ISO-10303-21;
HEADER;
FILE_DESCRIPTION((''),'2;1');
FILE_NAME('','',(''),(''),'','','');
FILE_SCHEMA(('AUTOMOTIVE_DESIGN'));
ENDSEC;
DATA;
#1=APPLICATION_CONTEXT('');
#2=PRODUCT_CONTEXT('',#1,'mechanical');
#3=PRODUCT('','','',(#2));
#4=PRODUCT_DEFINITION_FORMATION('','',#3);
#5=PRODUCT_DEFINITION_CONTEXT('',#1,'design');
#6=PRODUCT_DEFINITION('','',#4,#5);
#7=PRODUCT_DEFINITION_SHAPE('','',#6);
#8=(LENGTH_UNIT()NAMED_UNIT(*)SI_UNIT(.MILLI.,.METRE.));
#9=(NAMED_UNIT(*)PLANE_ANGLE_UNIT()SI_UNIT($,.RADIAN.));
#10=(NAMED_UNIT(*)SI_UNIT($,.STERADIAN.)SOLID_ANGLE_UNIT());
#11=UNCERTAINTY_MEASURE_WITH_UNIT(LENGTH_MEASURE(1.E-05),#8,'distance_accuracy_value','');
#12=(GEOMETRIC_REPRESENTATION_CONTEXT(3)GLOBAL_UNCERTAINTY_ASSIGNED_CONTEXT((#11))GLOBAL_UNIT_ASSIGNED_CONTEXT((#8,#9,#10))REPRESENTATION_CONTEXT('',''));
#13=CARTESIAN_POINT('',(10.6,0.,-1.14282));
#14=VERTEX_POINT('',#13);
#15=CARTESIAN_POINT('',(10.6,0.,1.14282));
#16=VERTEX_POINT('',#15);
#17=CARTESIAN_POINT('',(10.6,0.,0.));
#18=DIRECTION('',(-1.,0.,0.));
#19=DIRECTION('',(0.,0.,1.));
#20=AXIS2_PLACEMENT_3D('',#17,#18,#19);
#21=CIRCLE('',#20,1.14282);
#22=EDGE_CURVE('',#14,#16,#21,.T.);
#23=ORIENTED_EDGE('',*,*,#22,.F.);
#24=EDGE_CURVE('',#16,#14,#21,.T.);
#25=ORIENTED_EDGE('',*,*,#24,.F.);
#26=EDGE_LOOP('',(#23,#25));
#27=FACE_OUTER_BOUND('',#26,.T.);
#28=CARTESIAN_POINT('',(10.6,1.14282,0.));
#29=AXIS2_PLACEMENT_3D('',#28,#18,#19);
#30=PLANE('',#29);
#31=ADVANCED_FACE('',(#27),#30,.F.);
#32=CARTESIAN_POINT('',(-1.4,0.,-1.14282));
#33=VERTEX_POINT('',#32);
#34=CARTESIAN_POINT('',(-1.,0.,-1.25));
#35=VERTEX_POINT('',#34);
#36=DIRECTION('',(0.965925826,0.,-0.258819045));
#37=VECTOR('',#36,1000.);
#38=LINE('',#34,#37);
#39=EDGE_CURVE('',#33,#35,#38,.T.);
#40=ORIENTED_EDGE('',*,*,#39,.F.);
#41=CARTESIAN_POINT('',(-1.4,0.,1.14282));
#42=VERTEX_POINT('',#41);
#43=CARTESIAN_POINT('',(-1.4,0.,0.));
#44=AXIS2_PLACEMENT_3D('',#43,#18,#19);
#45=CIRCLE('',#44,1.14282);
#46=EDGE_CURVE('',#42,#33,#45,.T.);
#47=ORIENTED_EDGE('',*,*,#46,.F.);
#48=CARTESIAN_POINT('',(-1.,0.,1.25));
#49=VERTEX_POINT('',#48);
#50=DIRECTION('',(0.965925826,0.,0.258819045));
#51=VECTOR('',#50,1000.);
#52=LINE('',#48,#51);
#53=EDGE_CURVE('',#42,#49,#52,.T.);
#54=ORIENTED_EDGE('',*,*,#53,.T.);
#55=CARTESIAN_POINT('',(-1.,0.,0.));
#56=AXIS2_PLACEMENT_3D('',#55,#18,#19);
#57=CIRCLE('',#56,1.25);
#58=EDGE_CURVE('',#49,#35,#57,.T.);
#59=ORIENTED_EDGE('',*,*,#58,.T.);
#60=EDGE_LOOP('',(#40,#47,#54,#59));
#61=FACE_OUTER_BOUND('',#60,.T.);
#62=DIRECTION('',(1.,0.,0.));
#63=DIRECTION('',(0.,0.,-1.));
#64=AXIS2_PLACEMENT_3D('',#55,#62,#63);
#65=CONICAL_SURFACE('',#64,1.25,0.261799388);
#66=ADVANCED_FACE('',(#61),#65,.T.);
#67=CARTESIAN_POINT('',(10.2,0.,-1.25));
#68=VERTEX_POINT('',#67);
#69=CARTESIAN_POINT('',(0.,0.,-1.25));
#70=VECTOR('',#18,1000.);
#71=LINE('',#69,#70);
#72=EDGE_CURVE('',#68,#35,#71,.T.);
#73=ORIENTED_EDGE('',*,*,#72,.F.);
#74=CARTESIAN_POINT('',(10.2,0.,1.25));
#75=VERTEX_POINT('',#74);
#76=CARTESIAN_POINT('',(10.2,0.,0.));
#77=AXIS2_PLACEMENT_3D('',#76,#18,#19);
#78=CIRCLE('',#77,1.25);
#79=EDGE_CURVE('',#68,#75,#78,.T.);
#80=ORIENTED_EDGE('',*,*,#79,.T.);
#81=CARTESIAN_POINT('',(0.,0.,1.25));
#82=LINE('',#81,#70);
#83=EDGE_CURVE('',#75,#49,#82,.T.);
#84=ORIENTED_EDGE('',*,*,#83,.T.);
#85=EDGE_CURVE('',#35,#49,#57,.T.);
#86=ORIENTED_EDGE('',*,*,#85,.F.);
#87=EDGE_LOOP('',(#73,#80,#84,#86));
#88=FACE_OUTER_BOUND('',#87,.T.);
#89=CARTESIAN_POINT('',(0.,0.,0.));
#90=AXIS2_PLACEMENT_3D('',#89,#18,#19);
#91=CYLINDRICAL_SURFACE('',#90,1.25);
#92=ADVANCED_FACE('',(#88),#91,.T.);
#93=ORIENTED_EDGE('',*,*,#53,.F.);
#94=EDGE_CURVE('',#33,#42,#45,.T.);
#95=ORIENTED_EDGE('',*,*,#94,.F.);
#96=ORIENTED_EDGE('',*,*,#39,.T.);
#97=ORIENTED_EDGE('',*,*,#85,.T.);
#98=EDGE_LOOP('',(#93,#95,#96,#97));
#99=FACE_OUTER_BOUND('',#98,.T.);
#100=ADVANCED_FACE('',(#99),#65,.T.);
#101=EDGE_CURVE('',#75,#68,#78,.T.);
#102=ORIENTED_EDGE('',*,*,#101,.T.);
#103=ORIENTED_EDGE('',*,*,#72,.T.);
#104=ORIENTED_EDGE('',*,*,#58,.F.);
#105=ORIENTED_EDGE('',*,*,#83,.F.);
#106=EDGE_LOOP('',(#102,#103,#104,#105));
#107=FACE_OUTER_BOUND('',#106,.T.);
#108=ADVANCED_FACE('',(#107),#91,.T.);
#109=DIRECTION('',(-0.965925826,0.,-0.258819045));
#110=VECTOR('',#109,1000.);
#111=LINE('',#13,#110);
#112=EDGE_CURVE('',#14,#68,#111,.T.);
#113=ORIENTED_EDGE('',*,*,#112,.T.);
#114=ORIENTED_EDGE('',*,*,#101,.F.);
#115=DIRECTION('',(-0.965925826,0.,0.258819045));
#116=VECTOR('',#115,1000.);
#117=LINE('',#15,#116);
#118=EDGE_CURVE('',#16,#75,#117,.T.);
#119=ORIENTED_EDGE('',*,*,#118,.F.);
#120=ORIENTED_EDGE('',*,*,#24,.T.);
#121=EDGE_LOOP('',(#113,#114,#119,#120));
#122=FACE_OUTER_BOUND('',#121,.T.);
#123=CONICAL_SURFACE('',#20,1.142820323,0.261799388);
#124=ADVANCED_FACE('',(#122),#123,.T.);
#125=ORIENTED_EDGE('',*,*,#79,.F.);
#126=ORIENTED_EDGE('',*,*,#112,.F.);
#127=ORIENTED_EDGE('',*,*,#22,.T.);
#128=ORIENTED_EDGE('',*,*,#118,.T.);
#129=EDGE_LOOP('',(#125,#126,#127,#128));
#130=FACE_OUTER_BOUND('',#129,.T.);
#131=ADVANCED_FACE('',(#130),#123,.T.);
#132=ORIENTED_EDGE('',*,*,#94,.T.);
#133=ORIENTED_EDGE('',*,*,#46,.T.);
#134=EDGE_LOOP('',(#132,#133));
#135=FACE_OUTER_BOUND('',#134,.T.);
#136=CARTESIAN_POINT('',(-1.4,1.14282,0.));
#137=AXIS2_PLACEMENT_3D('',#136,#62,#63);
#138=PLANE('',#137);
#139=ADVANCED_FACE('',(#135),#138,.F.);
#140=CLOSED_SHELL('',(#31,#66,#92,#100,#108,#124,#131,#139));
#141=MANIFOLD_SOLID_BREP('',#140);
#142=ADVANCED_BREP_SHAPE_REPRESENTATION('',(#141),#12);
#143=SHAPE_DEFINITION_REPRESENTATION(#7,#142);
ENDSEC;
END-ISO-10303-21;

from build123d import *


with BuildPart() as part:
    # Sketch1 → Base-Revolve (revolve)
    with BuildSketch(Plane.XY, mode=Mode.PRIVATE) as base_revolve_sk:
        Polygon((-1.4, 0), (10.6, 0), (10.6, 1.142820323), (10.2, 1.25), (-1, 1.25), (-1.4, 1.142820323), align=None)
    revolve(base_revolve_sk.sketch.rotate(Axis((0, 0, 0), (1, 0, 0)), 90), axis=Axis((0, 0, 0), (1, 0, 0)))


solid = part.part
